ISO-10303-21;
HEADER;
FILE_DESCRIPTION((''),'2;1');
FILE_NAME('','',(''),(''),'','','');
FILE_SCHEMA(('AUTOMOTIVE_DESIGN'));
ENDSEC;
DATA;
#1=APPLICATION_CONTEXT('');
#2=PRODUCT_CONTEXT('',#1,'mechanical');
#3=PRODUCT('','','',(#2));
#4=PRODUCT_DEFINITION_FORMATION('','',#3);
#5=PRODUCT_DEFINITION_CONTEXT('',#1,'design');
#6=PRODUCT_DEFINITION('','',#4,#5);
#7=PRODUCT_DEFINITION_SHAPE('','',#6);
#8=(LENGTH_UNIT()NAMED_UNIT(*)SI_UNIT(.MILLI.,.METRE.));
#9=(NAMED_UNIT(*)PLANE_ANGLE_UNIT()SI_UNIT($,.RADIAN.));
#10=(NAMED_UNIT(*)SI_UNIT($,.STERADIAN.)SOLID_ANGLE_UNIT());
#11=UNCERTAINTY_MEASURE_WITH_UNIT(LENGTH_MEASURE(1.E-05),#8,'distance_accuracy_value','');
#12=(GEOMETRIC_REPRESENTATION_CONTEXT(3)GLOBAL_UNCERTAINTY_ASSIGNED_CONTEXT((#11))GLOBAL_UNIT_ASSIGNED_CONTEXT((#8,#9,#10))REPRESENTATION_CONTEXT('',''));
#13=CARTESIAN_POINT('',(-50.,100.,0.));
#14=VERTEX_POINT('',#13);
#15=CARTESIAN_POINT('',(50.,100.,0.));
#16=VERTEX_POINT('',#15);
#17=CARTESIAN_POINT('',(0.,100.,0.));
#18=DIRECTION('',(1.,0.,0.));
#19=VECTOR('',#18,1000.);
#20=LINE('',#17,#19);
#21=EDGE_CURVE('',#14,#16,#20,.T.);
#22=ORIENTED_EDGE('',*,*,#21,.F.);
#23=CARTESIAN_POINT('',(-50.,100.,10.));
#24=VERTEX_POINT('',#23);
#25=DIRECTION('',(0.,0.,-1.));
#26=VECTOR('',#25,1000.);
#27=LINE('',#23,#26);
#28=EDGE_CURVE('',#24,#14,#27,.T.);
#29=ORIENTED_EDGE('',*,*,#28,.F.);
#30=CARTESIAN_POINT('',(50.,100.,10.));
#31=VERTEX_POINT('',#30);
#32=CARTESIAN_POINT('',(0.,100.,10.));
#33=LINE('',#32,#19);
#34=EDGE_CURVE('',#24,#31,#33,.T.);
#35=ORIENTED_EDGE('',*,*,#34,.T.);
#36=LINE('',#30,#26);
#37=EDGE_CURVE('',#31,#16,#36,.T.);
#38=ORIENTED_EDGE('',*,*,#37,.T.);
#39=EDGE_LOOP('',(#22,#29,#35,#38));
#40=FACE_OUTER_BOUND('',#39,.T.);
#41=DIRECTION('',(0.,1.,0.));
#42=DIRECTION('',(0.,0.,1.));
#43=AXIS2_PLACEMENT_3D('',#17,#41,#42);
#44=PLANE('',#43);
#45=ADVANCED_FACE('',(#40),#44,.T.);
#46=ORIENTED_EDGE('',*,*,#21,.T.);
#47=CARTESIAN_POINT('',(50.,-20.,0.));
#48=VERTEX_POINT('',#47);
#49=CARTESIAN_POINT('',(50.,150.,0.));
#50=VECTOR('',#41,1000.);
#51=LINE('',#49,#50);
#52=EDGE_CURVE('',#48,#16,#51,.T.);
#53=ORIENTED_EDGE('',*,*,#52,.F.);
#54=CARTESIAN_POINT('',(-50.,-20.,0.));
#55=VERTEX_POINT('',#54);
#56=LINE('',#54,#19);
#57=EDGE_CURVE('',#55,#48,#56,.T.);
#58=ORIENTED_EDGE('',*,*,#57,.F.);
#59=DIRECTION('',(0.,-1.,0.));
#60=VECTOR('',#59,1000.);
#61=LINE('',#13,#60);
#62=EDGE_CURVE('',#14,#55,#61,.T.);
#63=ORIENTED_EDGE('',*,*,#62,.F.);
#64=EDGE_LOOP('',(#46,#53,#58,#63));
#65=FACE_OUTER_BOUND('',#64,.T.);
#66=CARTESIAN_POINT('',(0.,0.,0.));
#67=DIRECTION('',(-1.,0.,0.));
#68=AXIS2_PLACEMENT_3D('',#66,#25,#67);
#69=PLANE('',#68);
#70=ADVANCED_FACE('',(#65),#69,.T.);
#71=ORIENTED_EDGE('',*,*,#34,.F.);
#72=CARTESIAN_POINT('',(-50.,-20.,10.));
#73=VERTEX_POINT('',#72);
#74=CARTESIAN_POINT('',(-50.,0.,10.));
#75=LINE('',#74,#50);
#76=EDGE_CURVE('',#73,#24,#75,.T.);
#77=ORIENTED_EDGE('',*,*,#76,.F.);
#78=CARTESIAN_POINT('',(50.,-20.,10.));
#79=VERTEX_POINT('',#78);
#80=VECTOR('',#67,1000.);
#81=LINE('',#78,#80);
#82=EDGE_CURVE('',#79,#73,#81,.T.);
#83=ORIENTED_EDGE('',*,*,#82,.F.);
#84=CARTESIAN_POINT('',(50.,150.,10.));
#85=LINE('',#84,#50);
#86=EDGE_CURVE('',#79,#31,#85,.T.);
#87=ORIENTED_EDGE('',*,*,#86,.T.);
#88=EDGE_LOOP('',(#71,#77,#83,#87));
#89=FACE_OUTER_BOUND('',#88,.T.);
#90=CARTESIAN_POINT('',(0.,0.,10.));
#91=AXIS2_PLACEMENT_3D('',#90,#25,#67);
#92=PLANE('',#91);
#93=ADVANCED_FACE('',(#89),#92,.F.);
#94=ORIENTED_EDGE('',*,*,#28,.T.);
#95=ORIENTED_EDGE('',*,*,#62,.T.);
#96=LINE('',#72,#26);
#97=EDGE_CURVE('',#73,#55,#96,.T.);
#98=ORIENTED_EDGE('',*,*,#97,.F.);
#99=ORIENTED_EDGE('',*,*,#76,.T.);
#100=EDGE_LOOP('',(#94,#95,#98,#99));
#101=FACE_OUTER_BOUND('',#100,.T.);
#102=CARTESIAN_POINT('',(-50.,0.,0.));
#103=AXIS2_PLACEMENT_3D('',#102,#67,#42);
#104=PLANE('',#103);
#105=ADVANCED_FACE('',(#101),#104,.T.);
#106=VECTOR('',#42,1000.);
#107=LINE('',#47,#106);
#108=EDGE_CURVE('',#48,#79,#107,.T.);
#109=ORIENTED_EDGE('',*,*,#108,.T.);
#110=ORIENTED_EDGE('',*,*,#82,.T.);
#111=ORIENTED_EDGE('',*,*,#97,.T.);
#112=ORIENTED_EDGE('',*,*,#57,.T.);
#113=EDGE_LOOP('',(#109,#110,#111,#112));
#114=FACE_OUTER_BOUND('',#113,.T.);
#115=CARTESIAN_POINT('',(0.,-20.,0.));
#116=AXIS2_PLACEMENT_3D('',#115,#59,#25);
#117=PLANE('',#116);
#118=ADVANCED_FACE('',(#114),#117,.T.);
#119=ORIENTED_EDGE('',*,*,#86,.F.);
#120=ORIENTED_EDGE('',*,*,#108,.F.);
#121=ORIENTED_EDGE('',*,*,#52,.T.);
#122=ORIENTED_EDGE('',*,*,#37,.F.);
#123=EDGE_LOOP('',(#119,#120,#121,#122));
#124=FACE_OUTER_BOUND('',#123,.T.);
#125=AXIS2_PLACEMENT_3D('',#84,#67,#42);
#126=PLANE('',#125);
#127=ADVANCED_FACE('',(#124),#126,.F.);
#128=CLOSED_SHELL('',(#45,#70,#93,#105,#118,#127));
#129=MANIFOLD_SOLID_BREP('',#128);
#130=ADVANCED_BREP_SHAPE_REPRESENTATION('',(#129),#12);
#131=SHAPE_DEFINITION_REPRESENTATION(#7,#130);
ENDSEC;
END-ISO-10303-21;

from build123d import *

# Parameters (mm, degrees)
SKETCH_1_W          = 50
SKETCH_1_H          = 150
EXTRUDE_1_DEPTH     = 10
SKETCH_2_W          = 70
SKETCH_2_H          = 30
CUT_EXTRUDE_1_DEPTH = 50
SKETCH_3_W          = 10
SKETCH_3_H          = 100
EXTRUDE_2_DEPTH     = 50
SKETCH_4_W          = 100
SKETCH_4_H          = 10
EXTRUDE_3_DEPTH     = 20


with BuildPart() as part:
    # 草图1 → 凸台-拉伸1 (new body)
    with BuildSketch(Plane.XY):
        with Locations((25, 75)):
            Rectangle(SKETCH_1_W, SKETCH_1_H)
    extrude(amount=EXTRUDE_1_DEPTH)

    # 草图2 → 切除-拉伸1 (cut)
    with BuildSketch(Plane(origin=(0, 150, 0), x_dir=(1, 0, 0), z_dir=(0, 1, 0))):
        with Locations((25, -5)):
            Rectangle(SKETCH_2_W, SKETCH_2_H)
    extrude(amount=-CUT_EXTRUDE_1_DEPTH, mode=Mode.SUBTRACT)

    # 草图3 → 凸台-拉伸2 (add)
    with BuildSketch(Plane.ZY):
        with Locations((5, 50)):
            Rectangle(SKETCH_3_W, SKETCH_3_H)
    extrude(amount=EXTRUDE_2_DEPTH)

    # 草图4 → 凸台-拉伸3 (add)
    with BuildSketch(Plane.XZ):
        with Locations((0, 5)):
            Rectangle(SKETCH_4_W, SKETCH_4_H)
    extrude(amount=EXTRUDE_3_DEPTH)


solid = part.part
